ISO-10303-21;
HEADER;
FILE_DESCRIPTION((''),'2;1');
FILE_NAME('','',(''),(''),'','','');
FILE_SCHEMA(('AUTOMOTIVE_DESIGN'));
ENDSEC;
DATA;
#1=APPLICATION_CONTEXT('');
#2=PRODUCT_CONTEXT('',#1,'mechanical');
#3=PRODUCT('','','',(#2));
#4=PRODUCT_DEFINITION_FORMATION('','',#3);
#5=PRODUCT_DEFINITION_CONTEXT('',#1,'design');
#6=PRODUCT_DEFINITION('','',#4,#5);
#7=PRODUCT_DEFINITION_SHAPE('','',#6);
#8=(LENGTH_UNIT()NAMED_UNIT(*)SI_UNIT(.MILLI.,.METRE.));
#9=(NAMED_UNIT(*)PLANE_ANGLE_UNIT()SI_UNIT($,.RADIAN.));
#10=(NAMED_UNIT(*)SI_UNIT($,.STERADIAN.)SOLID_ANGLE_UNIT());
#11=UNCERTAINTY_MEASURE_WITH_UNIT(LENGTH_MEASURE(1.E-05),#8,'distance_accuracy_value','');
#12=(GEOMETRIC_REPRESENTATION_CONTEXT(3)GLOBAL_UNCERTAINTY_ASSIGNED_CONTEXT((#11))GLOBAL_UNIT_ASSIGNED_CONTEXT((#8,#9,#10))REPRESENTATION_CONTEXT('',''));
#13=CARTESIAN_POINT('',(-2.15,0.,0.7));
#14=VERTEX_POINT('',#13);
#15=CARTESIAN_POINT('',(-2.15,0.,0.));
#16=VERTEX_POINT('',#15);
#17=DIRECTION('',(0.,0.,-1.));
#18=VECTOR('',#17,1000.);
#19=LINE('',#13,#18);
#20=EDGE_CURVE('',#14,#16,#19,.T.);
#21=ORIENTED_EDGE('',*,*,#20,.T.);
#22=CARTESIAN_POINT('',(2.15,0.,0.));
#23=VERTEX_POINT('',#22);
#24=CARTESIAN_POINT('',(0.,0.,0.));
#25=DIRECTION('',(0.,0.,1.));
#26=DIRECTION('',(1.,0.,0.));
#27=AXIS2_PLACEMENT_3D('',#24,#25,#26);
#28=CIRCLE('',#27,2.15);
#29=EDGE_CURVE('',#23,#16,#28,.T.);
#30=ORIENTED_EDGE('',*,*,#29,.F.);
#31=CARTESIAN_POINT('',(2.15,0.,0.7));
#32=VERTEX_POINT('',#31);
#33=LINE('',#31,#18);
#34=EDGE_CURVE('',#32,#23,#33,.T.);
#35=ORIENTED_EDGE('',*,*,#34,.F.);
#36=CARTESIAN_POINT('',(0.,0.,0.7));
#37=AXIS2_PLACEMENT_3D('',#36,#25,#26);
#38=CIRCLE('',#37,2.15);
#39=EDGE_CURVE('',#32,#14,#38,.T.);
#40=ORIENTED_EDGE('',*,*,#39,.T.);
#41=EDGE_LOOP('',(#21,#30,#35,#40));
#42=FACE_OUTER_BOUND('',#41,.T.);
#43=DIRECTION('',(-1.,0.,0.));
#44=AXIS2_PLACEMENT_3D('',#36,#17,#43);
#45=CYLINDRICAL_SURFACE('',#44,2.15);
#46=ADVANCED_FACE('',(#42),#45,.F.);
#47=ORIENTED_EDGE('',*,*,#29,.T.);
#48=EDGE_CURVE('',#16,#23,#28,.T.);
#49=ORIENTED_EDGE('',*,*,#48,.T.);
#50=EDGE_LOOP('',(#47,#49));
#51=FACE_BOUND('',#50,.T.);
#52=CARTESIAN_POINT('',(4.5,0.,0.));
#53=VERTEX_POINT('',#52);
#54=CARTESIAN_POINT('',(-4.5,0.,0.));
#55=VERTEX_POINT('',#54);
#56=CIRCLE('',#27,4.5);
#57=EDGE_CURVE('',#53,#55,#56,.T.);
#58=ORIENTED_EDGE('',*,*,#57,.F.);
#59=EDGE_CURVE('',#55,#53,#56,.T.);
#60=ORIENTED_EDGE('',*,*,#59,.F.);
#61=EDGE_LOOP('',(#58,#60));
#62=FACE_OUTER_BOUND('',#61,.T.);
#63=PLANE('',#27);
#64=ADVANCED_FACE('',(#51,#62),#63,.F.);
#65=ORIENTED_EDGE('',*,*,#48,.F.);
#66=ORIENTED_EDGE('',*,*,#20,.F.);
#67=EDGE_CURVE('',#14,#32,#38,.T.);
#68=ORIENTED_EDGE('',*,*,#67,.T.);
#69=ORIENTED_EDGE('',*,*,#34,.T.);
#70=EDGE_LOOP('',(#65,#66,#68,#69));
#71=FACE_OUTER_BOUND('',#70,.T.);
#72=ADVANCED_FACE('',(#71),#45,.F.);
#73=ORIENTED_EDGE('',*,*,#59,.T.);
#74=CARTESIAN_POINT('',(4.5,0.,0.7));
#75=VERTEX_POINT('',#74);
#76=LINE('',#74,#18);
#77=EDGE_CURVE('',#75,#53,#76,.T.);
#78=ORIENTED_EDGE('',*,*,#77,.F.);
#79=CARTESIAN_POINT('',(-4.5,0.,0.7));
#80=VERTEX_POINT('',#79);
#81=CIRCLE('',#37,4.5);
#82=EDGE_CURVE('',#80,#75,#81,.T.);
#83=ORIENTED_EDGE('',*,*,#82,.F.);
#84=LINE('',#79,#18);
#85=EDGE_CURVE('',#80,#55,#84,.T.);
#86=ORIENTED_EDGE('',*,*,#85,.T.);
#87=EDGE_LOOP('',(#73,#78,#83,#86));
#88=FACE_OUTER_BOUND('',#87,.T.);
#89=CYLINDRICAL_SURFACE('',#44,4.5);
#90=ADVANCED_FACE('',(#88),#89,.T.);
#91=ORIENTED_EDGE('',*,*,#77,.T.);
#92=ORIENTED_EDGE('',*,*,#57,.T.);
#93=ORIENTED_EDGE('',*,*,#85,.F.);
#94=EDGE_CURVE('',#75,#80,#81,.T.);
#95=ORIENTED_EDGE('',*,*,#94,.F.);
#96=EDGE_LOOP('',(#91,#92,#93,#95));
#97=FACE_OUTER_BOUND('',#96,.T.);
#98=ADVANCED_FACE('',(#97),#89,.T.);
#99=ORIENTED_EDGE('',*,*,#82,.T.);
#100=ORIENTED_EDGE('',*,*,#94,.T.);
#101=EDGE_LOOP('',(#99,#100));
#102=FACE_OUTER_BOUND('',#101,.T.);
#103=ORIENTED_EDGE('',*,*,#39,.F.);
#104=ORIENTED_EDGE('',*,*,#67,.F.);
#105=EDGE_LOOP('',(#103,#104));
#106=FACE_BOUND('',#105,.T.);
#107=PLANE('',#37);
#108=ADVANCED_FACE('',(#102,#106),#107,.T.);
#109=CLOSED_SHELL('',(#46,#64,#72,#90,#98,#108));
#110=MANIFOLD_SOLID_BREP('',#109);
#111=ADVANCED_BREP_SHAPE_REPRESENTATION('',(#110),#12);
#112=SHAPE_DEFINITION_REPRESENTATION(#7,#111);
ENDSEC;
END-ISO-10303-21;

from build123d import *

# Parameters (mm, degrees)
SKETCH1_R           = 4.5
SKETCH1_R_2         = 2.15
BOSS_EXTRUDE1_DEPTH = 0.7


with BuildPart() as part:
    # Sketch1 → Boss-Extrude1 (new body)
    with BuildSketch(Plane.XY):
        Circle(SKETCH1_R)
        Circle(SKETCH1_R_2, mode=Mode.SUBTRACT)
    extrude(amount=BOSS_EXTRUDE1_DEPTH)


solid = part.part
